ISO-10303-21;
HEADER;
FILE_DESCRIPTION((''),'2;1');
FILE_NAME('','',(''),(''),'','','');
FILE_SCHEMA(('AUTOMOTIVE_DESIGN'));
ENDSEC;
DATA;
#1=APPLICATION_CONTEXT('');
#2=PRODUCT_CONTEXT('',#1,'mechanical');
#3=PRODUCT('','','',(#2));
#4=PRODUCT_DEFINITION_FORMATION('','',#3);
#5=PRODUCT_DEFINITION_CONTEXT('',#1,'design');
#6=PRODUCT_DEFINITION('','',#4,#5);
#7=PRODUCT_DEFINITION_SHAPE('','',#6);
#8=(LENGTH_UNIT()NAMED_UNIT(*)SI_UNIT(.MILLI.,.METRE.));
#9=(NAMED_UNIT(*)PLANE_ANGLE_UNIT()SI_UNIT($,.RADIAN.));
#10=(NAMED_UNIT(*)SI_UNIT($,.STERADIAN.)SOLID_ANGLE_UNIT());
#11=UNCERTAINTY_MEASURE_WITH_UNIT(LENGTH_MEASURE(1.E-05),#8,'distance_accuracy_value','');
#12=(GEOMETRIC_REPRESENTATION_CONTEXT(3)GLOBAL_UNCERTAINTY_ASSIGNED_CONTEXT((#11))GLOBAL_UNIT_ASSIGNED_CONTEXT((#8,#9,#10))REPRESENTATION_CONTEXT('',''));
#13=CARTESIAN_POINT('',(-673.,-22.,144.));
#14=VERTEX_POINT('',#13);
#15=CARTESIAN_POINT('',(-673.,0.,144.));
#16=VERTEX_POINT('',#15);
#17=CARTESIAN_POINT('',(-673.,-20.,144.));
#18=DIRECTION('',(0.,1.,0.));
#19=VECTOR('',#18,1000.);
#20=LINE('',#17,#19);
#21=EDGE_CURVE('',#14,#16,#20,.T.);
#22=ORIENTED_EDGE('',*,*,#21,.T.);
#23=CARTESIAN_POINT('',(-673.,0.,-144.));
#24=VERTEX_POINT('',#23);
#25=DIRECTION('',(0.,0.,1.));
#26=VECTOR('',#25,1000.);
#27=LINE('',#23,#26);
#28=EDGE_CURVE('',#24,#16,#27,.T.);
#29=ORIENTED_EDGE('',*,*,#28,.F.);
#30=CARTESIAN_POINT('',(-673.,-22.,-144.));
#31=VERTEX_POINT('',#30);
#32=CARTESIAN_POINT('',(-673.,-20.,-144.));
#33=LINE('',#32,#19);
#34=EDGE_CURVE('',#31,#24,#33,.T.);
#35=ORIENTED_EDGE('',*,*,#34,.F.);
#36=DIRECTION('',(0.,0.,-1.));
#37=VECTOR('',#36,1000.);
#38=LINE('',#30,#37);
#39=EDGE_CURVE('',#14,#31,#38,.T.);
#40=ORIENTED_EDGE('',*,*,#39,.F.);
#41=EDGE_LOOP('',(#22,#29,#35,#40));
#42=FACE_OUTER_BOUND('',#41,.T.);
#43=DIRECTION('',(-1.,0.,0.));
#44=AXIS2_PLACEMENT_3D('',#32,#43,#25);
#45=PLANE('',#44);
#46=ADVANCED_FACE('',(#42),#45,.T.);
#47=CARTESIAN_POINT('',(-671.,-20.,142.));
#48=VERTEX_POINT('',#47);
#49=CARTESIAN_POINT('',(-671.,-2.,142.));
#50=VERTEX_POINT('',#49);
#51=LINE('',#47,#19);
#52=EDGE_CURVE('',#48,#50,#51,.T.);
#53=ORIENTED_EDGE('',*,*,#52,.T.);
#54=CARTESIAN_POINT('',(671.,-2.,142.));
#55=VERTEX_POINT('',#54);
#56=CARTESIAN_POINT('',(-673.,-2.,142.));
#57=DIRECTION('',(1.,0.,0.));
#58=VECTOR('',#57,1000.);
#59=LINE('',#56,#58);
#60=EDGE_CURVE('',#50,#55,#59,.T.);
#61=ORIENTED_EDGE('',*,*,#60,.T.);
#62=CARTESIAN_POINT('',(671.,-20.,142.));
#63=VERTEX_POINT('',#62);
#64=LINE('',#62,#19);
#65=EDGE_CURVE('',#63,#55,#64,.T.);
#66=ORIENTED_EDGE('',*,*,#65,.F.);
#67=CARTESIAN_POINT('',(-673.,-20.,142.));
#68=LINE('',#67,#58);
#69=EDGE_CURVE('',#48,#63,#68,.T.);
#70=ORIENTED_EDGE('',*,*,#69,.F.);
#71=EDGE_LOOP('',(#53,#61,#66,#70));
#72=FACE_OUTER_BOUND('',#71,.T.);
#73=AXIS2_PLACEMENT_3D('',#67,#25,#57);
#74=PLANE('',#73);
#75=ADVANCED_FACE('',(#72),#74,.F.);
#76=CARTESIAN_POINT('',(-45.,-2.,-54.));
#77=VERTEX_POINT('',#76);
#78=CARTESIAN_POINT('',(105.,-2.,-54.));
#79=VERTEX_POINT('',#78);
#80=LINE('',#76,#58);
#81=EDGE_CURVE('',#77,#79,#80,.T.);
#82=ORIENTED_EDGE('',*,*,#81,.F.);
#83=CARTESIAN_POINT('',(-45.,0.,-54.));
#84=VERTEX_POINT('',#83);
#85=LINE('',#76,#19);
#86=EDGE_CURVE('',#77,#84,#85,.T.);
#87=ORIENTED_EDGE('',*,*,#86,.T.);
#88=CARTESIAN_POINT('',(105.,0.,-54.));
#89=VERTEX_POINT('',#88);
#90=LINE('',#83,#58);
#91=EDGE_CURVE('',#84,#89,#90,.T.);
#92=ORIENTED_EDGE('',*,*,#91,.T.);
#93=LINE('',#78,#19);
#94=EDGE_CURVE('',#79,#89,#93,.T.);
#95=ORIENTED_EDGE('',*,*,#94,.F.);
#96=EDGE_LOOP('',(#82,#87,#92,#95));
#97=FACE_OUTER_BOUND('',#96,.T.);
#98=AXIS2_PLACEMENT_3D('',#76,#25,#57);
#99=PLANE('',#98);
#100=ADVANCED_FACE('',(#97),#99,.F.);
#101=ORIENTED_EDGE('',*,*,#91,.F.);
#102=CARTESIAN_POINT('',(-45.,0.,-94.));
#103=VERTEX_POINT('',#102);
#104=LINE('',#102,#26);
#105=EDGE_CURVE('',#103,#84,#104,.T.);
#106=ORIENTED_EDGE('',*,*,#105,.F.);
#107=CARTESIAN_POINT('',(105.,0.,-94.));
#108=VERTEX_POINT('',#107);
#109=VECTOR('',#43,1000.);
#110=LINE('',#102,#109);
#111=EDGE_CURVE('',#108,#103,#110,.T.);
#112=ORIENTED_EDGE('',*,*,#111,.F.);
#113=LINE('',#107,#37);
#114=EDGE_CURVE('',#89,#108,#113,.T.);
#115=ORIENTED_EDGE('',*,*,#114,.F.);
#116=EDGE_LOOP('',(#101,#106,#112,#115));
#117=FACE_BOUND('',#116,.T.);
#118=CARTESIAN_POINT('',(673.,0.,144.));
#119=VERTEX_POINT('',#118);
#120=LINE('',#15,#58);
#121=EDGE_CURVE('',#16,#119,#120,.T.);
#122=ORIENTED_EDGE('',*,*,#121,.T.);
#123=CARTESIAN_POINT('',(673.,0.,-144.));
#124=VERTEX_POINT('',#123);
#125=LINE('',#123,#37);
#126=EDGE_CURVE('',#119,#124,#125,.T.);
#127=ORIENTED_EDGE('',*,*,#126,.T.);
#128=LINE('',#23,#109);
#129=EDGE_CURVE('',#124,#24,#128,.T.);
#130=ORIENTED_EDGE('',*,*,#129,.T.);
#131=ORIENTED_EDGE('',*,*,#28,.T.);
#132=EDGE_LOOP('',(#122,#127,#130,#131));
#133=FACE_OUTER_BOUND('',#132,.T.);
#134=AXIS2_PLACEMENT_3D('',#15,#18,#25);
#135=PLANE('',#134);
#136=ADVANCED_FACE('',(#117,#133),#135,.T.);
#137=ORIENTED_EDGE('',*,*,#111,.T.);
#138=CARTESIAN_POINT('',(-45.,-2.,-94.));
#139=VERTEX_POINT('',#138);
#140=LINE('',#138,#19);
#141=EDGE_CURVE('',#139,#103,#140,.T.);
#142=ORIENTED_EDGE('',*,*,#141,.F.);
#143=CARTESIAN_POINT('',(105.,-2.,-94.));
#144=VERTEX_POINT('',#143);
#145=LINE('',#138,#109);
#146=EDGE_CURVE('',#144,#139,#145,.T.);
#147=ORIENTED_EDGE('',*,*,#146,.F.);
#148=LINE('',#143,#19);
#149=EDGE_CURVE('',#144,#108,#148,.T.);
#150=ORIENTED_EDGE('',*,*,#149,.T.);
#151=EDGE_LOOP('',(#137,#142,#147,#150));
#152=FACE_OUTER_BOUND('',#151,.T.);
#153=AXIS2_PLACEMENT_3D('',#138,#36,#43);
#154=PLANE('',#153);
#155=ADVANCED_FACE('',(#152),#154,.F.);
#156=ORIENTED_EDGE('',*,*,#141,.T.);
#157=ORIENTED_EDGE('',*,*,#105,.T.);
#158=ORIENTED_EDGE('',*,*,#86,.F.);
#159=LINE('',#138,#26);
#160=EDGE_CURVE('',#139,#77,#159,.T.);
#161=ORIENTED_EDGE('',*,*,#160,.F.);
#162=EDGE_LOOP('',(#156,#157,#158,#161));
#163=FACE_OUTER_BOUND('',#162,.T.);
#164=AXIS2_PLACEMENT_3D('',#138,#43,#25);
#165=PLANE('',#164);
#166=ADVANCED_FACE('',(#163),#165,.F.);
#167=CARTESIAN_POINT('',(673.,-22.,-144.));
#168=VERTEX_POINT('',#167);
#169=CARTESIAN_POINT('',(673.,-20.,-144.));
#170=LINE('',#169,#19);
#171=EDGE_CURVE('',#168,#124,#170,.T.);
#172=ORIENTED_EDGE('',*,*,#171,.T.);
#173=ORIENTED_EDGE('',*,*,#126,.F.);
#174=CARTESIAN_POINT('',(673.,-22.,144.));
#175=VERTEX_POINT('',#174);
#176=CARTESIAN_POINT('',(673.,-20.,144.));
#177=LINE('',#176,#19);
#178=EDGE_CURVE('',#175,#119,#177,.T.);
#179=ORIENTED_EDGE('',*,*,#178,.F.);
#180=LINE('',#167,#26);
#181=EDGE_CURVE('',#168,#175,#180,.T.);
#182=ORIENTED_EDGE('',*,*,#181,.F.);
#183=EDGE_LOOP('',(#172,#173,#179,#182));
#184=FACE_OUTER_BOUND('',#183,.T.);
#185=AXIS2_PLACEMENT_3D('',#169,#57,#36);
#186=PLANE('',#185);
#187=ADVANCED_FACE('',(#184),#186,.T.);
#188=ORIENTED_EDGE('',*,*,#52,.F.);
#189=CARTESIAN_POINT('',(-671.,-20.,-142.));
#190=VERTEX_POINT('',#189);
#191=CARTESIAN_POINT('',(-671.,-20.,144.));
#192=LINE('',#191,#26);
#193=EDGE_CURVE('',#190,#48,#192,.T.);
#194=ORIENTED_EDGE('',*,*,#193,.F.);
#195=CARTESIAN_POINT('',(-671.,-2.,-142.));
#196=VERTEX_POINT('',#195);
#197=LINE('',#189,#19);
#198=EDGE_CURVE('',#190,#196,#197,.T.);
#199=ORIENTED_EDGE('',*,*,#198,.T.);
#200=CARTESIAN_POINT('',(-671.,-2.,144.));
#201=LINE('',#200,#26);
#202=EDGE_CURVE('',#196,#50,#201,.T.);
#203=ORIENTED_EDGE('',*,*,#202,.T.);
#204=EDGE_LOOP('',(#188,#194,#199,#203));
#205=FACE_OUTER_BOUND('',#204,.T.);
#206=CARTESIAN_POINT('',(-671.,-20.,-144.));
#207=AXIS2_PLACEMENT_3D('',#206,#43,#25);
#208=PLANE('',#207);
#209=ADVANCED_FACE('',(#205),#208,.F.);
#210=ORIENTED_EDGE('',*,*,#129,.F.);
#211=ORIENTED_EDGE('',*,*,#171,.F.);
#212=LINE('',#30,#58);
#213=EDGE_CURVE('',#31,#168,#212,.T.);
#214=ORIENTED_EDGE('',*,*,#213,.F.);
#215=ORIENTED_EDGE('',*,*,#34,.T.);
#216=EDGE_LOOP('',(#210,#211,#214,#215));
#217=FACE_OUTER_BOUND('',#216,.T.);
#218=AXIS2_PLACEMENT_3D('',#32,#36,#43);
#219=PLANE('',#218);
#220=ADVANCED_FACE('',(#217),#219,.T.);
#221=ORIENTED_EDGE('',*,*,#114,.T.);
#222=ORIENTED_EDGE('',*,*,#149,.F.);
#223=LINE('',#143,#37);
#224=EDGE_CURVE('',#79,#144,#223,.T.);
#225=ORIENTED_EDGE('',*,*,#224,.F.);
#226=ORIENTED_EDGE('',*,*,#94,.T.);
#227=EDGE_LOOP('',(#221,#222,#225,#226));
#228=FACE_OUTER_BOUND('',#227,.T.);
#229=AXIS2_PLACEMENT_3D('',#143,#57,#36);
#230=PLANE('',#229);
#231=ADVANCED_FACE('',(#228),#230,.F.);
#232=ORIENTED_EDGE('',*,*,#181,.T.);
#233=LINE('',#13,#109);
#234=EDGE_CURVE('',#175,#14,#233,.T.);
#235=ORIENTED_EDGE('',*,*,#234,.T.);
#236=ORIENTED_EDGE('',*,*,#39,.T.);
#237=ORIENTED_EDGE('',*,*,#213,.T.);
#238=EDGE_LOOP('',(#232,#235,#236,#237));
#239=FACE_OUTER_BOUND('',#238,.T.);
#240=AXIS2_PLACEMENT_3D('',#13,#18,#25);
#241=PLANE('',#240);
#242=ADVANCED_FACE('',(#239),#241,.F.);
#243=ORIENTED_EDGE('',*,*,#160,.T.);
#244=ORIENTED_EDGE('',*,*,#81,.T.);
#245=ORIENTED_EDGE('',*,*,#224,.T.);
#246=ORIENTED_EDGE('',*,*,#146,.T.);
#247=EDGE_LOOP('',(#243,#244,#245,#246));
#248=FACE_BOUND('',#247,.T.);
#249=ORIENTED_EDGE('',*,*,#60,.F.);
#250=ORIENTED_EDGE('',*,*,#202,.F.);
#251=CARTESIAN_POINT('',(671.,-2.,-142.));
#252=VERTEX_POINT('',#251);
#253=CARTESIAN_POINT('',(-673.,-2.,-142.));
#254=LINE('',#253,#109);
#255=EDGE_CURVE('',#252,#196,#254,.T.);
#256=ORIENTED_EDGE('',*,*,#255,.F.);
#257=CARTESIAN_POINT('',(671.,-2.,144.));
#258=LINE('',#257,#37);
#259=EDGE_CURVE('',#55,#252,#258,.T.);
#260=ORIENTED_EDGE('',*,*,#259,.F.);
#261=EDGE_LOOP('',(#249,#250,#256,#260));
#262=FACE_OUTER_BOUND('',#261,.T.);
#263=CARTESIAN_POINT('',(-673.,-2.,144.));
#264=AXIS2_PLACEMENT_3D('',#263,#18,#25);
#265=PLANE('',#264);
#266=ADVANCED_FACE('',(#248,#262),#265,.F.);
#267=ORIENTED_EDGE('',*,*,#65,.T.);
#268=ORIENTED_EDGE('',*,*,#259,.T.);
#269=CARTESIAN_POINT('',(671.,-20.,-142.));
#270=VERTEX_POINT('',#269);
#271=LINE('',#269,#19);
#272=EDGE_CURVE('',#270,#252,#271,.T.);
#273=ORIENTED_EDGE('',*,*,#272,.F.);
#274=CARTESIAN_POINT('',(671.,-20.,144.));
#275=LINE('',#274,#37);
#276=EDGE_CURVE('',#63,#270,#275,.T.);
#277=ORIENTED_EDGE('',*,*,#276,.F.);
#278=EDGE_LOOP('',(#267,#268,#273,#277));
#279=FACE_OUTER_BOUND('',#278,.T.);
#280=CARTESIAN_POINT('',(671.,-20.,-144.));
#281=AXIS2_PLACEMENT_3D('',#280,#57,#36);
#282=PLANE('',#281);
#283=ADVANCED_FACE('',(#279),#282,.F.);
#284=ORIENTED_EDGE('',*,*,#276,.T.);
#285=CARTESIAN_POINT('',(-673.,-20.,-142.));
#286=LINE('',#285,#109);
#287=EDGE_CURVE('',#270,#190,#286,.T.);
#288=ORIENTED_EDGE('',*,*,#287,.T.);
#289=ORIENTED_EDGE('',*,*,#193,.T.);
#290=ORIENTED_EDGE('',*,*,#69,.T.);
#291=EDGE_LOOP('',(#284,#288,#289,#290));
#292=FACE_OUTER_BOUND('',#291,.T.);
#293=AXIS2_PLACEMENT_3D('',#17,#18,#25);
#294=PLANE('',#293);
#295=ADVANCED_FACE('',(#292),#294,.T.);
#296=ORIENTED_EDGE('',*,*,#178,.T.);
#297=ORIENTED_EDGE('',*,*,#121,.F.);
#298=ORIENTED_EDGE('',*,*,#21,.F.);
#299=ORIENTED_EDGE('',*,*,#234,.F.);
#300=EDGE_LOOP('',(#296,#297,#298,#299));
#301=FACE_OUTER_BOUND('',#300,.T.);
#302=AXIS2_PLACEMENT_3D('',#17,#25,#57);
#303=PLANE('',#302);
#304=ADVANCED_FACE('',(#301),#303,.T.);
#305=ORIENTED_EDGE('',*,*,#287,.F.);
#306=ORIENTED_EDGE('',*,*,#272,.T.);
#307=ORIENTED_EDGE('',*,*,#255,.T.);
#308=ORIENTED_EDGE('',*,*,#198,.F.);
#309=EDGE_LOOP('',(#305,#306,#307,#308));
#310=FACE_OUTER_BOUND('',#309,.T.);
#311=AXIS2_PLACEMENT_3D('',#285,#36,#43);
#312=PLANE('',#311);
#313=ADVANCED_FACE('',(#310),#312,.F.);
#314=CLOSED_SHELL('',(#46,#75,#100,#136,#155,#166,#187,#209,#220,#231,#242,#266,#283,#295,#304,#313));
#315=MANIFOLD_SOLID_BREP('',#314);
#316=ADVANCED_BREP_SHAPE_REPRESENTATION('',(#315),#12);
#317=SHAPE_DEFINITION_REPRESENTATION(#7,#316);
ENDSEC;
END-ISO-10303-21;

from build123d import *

# Parameters (mm, degrees)
SKETCH_1_W          = 1346
SKETCH_1_H          = 288
EXTRUDE_1_DEPTH     = 20
SHELL_1_T           = -2
SKETCH_2_W          = 1346
SKETCH_2_H          = 288
EXTRUDE_2_DEPTH     = 2
SKETCH_4_W          = 150
SKETCH_4_H          = 40
CUT_EXTRUDE_1_DEPTH = 2


with BuildPart() as part:
    # 草图1 → 凸台-拉伸1 (new body)
    with BuildSketch(Plane(origin=(0, 0, 0), x_dir=(1, 0, 0), z_dir=(0, 1, 0))):
        Rectangle(SKETCH_1_W, SKETCH_1_H)
    extrude(amount=-EXTRUDE_1_DEPTH)

    # 抽壳1
    shell_1_openings = [part.faces().sort_by_distance(p)[0] for p in [
        (0, -20, 0),
    ]]
    offset(amount=SHELL_1_T, openings=shell_1_openings, kind=Kind.INTERSECTION)

    # 草图2 → 凸台-拉伸2 (add)
    with BuildSketch(Plane.XZ.offset(20)):
        Rectangle(SKETCH_2_W, SKETCH_2_H)
    extrude(amount=EXTRUDE_2_DEPTH)

    # 草图4 → 切除-拉伸1 (cut)
    with BuildSketch(Plane(origin=(0, 0, 0), x_dir=(1, 0, 0), z_dir=(0, 1, 0))):
        with Locations((30, 74)):
            Rectangle(SKETCH_4_W, SKETCH_4_H)
    extrude(amount=-CUT_EXTRUDE_1_DEPTH, mode=Mode.SUBTRACT)


solid = part.part
